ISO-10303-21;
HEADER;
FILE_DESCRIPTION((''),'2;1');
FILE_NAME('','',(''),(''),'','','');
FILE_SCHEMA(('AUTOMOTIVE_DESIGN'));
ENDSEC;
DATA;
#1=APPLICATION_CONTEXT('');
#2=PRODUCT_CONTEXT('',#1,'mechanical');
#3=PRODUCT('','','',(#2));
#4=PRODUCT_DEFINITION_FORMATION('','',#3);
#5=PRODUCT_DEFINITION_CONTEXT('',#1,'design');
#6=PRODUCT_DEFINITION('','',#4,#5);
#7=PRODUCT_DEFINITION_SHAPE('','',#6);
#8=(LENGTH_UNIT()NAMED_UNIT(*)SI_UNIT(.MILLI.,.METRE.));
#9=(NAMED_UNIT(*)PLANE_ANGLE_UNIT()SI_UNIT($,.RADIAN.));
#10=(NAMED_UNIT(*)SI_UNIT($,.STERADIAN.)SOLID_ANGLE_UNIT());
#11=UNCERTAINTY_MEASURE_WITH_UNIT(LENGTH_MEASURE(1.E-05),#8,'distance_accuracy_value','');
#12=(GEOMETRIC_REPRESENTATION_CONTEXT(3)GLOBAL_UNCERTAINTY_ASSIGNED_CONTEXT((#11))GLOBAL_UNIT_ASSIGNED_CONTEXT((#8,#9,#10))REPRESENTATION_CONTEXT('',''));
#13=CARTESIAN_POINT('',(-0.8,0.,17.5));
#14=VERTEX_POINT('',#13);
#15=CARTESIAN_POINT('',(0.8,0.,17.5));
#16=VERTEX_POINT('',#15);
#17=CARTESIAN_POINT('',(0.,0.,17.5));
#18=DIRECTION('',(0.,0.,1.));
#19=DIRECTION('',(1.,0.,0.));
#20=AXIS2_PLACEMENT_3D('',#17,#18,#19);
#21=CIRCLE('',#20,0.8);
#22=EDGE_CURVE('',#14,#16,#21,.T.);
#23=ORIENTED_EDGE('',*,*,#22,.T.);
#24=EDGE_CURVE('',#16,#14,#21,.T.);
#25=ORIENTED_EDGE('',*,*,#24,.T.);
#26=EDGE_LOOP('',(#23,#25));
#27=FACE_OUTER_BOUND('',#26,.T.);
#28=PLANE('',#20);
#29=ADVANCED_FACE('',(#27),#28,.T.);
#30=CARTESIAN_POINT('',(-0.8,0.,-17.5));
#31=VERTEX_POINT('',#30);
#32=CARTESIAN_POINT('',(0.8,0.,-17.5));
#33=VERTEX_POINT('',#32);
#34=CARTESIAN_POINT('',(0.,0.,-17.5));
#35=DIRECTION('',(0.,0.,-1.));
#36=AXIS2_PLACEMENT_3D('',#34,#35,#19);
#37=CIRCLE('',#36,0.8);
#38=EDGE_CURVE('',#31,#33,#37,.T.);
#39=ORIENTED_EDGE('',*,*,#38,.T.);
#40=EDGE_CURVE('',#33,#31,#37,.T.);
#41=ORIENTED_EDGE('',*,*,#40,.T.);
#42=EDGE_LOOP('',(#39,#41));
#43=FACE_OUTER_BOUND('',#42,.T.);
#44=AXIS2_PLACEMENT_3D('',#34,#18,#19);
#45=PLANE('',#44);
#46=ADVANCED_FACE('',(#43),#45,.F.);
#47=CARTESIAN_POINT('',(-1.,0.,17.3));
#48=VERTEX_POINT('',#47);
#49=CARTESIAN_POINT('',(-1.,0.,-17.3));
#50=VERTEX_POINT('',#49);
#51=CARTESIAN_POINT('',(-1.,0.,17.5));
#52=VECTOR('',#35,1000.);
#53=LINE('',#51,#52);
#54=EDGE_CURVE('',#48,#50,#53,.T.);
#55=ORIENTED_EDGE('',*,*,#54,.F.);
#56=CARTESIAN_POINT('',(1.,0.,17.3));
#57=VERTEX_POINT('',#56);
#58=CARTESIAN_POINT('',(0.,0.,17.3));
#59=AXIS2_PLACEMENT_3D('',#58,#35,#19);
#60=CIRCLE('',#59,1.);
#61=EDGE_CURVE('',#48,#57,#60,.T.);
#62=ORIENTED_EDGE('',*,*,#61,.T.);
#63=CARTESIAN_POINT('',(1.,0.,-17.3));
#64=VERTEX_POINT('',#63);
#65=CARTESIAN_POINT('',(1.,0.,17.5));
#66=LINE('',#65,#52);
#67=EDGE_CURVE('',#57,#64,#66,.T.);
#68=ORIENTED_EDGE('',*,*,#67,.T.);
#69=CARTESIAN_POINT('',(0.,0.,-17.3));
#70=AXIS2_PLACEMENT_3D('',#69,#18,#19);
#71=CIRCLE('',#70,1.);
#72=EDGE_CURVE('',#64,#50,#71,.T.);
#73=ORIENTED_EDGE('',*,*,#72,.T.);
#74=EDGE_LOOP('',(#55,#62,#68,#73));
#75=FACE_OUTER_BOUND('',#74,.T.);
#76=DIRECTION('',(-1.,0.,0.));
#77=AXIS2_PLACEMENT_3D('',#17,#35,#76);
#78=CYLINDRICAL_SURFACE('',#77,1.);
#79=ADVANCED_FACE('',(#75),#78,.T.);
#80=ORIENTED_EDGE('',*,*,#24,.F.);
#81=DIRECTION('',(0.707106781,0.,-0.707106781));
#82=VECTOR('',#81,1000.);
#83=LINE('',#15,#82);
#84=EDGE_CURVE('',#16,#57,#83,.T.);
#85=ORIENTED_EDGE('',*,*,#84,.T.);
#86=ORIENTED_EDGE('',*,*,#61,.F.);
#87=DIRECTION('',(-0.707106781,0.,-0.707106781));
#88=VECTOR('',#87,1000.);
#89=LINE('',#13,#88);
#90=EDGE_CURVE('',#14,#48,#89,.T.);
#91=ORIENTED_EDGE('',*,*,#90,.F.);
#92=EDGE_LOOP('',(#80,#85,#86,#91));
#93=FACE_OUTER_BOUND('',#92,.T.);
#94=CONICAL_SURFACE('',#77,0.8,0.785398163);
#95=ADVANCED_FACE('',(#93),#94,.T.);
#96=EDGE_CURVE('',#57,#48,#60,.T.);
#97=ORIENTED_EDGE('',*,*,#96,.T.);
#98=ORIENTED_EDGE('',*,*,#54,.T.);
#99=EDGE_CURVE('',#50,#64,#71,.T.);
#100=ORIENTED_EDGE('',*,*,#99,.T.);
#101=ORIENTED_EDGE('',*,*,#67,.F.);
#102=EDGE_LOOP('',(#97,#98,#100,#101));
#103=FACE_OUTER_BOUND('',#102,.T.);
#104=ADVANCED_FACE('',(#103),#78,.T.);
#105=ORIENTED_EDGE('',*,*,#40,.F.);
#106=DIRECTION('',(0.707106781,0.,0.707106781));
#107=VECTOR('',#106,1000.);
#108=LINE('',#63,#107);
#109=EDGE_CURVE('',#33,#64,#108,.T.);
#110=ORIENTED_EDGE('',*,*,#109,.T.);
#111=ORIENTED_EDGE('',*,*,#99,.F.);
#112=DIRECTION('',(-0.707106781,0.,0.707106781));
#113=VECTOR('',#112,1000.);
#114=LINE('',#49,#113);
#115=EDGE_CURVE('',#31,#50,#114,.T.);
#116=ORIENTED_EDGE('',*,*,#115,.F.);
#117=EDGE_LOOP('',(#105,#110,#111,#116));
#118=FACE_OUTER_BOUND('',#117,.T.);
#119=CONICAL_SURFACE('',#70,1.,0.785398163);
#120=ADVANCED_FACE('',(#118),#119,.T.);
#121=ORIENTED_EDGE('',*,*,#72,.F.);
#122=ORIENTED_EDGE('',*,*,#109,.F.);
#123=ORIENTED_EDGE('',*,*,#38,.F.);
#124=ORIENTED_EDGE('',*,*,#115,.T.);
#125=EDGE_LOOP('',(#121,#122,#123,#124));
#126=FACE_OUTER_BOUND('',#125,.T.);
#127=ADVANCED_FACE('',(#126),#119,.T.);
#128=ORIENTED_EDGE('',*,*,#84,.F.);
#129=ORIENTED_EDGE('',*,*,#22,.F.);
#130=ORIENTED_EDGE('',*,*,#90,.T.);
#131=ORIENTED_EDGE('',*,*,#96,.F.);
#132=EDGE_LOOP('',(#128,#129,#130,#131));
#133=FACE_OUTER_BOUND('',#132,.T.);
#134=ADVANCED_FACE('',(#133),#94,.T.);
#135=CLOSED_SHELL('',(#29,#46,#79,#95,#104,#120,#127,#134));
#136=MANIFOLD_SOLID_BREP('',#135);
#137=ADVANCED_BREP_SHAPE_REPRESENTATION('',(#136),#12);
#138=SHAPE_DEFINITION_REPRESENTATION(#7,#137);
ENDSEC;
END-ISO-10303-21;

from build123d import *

# Parameters (mm, degrees)
SKETCH1_R           = 1
BOSS_EXTRUDE1_DEPTH = 17.5
CHAMFER1_SIZE       = 0.2


with BuildPart() as part:
    # Sketch1 → Boss-Extrude1 (new, symmetric)
    with BuildSketch(Plane.XY):
        Circle(SKETCH1_R)
    extrude(amount=BOSS_EXTRUDE1_DEPTH, both=True)

    # Chamfer1
    chamfer1_edges = [part.edges().sort_by_distance(p)[0] for p in [
        (-1, 0, -17.5),
        (-1, 0, 17.5),
    ]]
    chamfer(chamfer1_edges, length=CHAMFER1_SIZE)


solid = part.part
